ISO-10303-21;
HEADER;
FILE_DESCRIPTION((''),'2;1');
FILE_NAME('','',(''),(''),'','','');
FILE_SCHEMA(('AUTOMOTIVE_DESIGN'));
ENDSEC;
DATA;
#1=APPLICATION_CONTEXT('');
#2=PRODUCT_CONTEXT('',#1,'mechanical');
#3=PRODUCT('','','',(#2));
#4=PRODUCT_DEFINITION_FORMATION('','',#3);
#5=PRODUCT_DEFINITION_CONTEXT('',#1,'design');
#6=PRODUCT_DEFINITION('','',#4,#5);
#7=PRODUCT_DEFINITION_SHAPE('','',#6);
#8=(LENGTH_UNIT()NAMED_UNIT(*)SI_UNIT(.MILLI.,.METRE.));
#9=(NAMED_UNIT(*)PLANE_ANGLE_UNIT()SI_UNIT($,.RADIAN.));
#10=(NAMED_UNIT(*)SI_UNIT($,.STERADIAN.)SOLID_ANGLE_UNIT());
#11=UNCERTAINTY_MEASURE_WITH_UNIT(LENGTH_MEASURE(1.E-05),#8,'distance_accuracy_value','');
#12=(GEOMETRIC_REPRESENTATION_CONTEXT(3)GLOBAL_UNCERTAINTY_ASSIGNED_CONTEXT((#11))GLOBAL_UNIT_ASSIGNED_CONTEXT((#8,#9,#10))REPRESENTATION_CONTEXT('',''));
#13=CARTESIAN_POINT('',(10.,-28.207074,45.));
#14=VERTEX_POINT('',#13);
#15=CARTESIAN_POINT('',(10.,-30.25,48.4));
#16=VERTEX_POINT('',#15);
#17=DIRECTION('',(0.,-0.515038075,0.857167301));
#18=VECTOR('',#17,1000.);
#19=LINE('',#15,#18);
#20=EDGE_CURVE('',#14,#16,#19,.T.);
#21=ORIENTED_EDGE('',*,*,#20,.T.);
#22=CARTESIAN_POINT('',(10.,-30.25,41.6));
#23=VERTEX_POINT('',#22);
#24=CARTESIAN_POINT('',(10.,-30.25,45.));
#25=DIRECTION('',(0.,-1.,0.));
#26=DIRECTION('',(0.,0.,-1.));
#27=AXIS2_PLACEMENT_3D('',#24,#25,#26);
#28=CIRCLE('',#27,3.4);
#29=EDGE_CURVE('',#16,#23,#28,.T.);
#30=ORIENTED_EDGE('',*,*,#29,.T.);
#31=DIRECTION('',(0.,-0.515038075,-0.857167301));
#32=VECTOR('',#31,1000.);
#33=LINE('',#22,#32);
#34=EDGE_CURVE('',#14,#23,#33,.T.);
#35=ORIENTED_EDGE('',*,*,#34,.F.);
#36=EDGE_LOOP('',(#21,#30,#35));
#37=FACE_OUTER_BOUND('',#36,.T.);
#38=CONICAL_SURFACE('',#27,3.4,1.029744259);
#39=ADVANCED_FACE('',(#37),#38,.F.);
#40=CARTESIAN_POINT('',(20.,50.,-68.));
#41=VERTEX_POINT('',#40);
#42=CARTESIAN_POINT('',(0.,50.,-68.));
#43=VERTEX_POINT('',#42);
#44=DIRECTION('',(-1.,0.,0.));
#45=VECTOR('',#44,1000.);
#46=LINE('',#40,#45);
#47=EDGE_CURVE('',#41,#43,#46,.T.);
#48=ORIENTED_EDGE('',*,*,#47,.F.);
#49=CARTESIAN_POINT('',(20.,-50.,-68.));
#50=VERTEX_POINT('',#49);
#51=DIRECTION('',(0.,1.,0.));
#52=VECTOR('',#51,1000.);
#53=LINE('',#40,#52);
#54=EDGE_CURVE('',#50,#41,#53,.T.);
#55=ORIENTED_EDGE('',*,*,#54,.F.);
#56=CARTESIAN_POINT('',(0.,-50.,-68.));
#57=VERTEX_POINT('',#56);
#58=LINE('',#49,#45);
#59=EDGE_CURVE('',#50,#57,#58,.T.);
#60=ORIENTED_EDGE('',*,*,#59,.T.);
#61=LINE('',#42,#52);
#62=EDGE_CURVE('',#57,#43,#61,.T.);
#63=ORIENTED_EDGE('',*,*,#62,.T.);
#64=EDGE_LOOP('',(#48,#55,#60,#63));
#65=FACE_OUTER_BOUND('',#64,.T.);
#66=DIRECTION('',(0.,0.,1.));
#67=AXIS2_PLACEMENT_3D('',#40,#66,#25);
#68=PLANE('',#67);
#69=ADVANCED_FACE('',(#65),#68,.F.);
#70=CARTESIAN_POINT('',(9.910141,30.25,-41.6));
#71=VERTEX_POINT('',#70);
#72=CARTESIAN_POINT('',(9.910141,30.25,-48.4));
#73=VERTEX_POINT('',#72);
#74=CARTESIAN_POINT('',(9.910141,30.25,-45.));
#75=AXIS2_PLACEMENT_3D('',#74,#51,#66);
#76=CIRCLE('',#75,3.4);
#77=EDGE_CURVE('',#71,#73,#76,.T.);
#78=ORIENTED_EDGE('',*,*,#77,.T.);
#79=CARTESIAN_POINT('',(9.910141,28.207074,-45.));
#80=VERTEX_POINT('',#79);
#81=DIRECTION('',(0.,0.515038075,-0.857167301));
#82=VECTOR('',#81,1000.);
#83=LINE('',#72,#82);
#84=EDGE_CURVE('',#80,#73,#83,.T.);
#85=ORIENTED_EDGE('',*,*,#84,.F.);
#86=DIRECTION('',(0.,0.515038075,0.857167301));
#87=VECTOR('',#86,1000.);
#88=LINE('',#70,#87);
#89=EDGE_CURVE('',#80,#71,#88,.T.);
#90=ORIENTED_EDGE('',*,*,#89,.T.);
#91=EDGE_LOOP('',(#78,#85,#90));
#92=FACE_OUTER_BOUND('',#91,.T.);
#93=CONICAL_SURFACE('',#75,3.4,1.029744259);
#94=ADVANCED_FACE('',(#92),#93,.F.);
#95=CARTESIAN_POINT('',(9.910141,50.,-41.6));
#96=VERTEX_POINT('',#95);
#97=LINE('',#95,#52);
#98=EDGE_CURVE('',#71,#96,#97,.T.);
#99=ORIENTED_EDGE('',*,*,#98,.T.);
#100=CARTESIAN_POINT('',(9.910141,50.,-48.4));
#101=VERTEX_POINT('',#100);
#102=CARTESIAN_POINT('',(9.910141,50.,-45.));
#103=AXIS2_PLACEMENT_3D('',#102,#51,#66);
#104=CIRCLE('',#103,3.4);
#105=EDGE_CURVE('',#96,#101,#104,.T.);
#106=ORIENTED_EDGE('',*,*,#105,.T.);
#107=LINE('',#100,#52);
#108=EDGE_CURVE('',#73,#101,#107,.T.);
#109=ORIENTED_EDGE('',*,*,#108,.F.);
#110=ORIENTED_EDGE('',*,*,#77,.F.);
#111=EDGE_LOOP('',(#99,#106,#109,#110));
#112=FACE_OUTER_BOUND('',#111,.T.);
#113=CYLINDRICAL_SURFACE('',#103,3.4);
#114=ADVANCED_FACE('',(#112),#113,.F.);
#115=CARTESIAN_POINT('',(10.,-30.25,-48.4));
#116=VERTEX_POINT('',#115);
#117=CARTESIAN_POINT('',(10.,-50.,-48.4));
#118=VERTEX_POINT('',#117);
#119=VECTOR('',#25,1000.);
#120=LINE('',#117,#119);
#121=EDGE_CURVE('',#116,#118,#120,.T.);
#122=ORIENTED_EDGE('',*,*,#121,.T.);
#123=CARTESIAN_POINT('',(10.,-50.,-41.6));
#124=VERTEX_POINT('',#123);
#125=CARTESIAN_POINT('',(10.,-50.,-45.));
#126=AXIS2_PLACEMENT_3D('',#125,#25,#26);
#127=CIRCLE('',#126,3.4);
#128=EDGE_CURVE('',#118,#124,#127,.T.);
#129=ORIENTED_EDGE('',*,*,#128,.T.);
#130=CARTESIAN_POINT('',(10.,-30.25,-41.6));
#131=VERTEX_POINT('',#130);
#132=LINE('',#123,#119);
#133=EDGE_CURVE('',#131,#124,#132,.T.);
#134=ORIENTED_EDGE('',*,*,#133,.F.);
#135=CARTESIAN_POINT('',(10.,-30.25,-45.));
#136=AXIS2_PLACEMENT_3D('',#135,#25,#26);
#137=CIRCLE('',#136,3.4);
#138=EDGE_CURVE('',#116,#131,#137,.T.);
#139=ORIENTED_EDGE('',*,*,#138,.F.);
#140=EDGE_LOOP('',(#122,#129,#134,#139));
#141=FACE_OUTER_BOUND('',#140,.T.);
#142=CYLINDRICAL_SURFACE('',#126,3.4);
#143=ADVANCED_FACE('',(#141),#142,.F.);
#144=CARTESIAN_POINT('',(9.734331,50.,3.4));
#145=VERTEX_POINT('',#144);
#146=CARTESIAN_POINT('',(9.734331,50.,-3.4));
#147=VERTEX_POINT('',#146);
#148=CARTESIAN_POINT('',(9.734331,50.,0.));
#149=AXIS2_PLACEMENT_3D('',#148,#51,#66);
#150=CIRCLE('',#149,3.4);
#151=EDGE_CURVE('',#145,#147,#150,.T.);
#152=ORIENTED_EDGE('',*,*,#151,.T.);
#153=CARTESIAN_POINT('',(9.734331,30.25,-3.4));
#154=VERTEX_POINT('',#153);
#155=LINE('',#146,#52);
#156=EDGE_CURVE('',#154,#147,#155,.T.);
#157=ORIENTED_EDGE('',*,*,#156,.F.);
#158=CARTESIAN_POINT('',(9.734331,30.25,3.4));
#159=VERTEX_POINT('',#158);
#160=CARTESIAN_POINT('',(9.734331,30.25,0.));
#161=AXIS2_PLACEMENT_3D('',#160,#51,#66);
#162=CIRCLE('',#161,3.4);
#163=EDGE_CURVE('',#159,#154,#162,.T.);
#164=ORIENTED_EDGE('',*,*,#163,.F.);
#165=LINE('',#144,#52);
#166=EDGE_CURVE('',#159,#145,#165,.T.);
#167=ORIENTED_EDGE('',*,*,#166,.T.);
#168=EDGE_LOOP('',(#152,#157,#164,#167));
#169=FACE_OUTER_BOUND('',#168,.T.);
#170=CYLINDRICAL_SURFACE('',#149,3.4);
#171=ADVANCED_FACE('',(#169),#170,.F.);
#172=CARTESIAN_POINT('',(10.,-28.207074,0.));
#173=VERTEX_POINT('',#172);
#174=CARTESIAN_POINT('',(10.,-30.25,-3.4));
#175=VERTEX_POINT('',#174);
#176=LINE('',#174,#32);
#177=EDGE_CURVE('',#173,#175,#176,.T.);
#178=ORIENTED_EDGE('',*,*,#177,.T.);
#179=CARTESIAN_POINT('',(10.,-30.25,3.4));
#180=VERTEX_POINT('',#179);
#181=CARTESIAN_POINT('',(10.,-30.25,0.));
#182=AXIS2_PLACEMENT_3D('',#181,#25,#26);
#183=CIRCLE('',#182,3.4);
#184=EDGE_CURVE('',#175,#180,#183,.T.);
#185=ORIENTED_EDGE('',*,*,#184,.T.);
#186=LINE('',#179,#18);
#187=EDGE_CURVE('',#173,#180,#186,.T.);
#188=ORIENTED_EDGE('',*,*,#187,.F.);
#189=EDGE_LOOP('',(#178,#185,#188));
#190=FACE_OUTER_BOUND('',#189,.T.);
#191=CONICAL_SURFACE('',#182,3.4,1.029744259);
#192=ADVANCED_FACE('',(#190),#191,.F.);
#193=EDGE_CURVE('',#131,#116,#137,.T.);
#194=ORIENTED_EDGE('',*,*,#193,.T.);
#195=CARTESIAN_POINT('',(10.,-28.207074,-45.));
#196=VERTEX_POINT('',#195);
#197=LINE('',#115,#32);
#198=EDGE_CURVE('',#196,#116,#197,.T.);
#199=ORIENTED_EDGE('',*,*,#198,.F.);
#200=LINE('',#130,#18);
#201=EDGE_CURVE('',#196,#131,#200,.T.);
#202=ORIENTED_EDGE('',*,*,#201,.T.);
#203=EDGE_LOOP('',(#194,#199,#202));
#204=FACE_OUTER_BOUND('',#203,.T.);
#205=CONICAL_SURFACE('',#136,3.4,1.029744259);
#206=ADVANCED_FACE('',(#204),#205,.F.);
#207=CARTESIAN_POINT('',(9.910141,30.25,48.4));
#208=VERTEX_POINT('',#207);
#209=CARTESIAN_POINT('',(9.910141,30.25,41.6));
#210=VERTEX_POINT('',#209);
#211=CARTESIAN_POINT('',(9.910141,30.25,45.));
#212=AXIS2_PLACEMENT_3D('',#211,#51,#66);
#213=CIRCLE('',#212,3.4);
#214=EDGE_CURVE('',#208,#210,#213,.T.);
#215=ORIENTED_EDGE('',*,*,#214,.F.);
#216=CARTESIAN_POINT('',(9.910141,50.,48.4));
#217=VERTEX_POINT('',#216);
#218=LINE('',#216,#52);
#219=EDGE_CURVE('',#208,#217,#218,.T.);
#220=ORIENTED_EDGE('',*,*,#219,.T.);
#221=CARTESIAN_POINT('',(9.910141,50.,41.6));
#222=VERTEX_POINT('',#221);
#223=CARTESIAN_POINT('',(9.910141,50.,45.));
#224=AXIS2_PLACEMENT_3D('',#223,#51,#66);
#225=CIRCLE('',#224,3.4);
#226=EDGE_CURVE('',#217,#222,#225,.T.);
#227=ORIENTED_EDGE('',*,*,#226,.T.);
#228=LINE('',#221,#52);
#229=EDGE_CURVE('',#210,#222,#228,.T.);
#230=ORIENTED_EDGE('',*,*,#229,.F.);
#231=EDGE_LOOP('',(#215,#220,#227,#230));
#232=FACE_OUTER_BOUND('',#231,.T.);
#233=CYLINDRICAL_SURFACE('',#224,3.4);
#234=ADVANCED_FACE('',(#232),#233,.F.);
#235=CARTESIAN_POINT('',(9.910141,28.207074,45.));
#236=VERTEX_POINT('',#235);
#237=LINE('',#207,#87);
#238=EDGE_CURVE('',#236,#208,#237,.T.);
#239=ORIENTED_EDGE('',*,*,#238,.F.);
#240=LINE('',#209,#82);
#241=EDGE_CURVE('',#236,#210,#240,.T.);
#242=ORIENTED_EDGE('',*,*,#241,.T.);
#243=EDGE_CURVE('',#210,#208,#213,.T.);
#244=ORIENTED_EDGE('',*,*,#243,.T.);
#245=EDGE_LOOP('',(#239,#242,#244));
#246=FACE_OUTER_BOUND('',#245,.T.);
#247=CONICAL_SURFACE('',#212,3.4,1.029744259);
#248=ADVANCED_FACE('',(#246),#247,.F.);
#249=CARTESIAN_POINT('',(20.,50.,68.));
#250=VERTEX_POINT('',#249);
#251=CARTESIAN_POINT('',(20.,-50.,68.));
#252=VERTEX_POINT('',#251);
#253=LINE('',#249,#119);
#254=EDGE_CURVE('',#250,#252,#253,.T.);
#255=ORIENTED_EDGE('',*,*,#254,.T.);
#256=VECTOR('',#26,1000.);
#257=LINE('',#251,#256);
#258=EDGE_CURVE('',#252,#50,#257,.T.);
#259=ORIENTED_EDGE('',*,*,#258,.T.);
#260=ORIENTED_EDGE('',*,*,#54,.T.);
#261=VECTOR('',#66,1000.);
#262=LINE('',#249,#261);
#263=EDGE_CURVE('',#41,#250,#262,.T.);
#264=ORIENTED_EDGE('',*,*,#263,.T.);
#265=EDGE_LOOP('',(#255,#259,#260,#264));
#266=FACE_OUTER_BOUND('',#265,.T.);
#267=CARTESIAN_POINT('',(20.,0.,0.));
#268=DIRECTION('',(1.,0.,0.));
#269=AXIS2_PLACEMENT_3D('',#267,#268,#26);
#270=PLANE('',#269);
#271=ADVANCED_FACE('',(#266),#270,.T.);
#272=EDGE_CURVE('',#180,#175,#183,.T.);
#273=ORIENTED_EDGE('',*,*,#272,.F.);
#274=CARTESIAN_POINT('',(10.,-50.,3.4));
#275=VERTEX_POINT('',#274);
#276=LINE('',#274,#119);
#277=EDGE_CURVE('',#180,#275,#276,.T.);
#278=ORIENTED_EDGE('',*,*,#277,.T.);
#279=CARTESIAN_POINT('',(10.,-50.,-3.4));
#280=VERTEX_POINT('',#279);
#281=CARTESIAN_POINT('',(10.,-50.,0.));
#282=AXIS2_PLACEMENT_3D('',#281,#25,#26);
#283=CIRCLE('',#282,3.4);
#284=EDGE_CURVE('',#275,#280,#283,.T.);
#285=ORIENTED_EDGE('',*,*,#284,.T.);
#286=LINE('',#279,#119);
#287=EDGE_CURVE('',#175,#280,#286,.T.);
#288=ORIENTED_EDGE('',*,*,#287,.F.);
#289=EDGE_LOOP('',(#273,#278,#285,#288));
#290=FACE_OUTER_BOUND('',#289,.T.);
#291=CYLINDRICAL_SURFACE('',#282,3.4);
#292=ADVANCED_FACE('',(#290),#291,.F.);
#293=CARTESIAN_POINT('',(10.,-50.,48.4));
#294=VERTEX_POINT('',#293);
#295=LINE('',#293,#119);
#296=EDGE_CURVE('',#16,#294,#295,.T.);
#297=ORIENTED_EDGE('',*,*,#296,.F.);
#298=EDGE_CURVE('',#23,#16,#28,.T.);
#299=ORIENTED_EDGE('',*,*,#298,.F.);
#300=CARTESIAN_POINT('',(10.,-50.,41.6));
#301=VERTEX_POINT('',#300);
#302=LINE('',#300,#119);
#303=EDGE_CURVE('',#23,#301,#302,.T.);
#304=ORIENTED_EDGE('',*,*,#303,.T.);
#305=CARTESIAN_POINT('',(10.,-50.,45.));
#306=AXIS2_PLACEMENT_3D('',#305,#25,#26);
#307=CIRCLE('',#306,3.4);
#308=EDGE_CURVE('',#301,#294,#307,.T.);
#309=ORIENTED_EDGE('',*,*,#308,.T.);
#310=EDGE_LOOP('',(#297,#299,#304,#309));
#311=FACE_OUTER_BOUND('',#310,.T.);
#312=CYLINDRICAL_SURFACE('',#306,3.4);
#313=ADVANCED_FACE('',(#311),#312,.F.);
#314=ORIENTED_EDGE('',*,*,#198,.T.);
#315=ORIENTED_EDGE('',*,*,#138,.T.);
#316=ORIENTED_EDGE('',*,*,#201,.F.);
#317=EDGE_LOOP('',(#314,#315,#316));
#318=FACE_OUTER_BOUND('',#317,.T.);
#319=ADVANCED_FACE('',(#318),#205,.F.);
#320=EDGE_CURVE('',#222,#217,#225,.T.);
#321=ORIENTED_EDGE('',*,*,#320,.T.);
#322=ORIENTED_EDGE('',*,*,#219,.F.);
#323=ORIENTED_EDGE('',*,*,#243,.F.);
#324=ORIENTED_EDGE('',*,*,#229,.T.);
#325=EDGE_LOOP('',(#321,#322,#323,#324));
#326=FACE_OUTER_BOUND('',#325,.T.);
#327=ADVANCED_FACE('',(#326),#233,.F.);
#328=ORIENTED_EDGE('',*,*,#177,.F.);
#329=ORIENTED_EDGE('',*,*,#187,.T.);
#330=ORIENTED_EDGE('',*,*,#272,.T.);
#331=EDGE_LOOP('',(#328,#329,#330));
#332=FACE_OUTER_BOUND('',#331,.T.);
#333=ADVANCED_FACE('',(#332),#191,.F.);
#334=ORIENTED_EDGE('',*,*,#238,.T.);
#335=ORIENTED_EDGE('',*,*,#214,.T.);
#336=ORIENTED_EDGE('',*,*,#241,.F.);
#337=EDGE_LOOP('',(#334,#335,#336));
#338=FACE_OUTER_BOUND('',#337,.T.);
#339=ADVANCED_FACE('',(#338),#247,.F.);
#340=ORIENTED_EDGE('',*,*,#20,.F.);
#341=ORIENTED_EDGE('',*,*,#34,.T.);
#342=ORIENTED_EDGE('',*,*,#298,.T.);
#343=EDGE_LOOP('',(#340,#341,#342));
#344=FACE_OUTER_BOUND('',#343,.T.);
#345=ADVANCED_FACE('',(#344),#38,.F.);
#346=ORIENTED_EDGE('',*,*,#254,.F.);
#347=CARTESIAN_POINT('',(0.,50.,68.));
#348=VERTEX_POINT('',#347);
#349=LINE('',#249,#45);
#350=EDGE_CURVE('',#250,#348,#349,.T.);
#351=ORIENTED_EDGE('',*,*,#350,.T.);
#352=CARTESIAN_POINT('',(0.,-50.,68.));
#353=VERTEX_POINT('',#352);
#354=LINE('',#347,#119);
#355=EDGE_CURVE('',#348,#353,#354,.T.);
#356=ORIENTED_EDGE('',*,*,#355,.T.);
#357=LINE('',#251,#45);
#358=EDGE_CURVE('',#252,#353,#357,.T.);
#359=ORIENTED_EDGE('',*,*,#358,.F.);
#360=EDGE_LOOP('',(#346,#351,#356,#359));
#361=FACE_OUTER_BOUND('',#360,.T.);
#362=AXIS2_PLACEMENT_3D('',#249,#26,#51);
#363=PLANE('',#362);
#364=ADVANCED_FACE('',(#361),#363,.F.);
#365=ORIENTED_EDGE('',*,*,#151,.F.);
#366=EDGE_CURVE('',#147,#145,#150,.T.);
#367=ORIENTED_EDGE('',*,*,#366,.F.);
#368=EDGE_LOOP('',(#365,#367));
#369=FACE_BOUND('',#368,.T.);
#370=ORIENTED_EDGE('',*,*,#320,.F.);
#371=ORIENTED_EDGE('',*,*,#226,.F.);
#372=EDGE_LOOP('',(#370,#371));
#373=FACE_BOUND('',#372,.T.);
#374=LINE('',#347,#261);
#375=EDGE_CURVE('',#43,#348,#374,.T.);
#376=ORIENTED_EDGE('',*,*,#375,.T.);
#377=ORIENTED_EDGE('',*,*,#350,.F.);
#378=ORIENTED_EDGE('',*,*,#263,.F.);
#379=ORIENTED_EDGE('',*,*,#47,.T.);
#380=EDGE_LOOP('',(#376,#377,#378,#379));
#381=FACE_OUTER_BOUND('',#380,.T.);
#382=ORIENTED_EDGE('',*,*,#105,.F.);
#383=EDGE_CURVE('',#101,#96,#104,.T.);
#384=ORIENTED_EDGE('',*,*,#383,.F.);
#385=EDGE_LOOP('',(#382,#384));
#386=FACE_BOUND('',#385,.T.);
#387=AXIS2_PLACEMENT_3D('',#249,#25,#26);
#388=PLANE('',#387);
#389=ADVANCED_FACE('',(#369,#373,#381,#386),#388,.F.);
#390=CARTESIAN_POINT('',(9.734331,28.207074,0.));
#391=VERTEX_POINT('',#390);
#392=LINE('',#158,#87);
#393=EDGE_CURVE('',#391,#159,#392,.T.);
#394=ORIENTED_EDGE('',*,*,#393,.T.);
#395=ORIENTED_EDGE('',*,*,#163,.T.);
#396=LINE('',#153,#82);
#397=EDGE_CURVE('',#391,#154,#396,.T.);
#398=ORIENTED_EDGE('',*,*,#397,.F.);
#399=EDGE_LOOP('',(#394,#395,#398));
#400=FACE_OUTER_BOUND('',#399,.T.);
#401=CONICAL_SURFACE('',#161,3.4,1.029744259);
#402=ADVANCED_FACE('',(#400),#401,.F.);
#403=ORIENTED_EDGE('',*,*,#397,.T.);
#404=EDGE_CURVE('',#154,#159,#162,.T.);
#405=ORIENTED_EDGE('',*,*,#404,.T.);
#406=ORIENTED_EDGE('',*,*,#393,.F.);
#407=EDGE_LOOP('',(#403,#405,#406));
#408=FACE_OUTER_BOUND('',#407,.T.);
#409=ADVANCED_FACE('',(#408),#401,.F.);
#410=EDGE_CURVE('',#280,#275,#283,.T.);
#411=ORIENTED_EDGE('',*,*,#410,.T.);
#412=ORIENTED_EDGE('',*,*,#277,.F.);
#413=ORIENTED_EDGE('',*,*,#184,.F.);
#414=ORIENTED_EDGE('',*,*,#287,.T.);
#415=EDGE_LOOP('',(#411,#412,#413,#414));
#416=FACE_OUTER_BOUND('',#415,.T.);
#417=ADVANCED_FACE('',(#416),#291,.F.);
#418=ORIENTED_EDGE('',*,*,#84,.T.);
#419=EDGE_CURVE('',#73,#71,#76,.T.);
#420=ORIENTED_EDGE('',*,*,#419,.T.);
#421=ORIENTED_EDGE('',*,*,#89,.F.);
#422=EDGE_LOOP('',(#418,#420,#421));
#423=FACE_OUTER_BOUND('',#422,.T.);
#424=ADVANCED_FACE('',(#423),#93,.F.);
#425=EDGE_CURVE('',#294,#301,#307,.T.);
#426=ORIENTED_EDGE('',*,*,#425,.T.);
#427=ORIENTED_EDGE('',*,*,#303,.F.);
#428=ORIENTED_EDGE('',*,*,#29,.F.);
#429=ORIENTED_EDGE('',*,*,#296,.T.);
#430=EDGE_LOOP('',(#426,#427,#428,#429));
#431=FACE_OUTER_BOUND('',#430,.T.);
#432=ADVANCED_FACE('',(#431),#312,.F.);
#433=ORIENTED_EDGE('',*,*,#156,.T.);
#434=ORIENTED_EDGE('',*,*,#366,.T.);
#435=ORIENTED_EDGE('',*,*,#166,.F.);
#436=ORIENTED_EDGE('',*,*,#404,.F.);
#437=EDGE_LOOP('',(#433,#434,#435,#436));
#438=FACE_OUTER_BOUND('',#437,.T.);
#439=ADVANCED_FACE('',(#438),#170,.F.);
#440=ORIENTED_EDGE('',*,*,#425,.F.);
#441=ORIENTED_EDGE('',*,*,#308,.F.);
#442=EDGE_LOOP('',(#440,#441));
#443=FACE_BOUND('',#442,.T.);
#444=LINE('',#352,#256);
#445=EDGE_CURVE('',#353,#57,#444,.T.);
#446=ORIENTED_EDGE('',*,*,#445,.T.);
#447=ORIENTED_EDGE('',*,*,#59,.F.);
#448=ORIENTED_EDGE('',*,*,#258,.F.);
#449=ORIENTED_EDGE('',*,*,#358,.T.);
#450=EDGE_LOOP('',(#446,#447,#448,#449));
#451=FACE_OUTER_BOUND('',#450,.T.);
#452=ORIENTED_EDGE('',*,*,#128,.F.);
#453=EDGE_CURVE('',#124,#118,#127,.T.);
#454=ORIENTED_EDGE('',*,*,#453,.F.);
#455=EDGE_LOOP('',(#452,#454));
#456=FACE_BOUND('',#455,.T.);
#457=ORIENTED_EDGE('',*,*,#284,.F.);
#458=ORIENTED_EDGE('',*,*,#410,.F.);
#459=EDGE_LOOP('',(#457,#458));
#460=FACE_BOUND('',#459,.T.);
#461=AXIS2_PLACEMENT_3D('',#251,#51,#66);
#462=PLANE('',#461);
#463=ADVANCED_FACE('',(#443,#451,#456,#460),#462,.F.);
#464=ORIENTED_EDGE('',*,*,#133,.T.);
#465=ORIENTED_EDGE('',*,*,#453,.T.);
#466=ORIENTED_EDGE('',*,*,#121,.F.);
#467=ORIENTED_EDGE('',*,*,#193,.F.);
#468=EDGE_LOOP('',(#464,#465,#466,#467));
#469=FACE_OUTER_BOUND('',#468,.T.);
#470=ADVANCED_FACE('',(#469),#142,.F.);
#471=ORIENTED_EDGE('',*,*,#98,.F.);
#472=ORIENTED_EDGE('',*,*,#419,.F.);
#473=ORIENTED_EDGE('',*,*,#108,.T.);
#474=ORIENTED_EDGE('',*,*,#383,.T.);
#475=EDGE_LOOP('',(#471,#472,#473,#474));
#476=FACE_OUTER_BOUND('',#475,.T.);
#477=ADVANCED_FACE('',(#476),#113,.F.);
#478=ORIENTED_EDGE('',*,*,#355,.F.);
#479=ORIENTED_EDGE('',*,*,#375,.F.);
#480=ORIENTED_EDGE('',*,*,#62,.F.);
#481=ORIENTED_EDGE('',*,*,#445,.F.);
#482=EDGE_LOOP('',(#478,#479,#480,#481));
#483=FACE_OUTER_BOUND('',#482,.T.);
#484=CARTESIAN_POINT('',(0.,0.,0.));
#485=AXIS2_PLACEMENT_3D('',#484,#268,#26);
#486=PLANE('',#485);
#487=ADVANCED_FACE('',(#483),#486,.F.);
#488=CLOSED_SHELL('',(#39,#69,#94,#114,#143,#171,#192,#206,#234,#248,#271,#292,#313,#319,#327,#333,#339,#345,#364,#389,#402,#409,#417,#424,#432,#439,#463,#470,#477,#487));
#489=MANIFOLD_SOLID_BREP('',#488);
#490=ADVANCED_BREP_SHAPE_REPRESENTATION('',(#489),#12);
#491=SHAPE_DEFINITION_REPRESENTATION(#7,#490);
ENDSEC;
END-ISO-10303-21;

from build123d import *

# Parameters (mm, degrees)
SKETCH_1_W             = 136
SKETCH_1_H             = 100
EXTRUDE_1_DEPTH        = 20
HOLE_WIZARD_M8_1_D     = 6.8
HOLE_WIZARD_M8_1_DEPTH = 19.75
HOLE_WIZARD_M8_1_TIP   = 2.042926105
HOLE_WIZARD_M8_2_D     = 6.8
HOLE_WIZARD_M8_2_DEPTH = 19.75
HOLE_WIZARD_M8_2_TIP   = 2.042926105


with BuildPart() as part:
    # 草图1 → 凸台-拉伸1 (new body)
    with BuildSketch(Plane(origin=(0, 0, 0), x_dir=(0, 0, -1), z_dir=(1, 0, 0))):
        Rectangle(SKETCH_1_W, SKETCH_1_H)
    extrude(amount=EXTRUDE_1_DEPTH)

    # M8 螺纹孔1
    with Locations(Plane(origin=(0, 50, 0), x_dir=(1, 0, 0), z_dir=(0, 1, 0))):
        with Locations((9.910141203, 45), (9.910141203, -45), (9.734330512, 0)):
            Hole(HOLE_WIZARD_M8_1_D / 2, depth=HOLE_WIZARD_M8_1_DEPTH)
            with Locations((0, 0, -(HOLE_WIZARD_M8_1_DEPTH + HOLE_WIZARD_M8_1_TIP / 2))):  # 118° drill point
                Cone(0, HOLE_WIZARD_M8_1_D / 2, HOLE_WIZARD_M8_1_TIP, mode=Mode.SUBTRACT)

    # M8 螺纹孔2
    with Locations(Plane(origin=(0, -50, 0), x_dir=(-1, 0, 0), z_dir=(0, -1, 0))):
        with Locations((-10, 45), (-10, 0), (-10, -45)):
            Hole(HOLE_WIZARD_M8_2_D / 2, depth=HOLE_WIZARD_M8_2_DEPTH)
            with Locations((0, 0, -(HOLE_WIZARD_M8_2_DEPTH + HOLE_WIZARD_M8_2_TIP / 2))):  # 118° drill point
                Cone(0, HOLE_WIZARD_M8_2_D / 2, HOLE_WIZARD_M8_2_TIP, mode=Mode.SUBTRACT)


solid = part.part
